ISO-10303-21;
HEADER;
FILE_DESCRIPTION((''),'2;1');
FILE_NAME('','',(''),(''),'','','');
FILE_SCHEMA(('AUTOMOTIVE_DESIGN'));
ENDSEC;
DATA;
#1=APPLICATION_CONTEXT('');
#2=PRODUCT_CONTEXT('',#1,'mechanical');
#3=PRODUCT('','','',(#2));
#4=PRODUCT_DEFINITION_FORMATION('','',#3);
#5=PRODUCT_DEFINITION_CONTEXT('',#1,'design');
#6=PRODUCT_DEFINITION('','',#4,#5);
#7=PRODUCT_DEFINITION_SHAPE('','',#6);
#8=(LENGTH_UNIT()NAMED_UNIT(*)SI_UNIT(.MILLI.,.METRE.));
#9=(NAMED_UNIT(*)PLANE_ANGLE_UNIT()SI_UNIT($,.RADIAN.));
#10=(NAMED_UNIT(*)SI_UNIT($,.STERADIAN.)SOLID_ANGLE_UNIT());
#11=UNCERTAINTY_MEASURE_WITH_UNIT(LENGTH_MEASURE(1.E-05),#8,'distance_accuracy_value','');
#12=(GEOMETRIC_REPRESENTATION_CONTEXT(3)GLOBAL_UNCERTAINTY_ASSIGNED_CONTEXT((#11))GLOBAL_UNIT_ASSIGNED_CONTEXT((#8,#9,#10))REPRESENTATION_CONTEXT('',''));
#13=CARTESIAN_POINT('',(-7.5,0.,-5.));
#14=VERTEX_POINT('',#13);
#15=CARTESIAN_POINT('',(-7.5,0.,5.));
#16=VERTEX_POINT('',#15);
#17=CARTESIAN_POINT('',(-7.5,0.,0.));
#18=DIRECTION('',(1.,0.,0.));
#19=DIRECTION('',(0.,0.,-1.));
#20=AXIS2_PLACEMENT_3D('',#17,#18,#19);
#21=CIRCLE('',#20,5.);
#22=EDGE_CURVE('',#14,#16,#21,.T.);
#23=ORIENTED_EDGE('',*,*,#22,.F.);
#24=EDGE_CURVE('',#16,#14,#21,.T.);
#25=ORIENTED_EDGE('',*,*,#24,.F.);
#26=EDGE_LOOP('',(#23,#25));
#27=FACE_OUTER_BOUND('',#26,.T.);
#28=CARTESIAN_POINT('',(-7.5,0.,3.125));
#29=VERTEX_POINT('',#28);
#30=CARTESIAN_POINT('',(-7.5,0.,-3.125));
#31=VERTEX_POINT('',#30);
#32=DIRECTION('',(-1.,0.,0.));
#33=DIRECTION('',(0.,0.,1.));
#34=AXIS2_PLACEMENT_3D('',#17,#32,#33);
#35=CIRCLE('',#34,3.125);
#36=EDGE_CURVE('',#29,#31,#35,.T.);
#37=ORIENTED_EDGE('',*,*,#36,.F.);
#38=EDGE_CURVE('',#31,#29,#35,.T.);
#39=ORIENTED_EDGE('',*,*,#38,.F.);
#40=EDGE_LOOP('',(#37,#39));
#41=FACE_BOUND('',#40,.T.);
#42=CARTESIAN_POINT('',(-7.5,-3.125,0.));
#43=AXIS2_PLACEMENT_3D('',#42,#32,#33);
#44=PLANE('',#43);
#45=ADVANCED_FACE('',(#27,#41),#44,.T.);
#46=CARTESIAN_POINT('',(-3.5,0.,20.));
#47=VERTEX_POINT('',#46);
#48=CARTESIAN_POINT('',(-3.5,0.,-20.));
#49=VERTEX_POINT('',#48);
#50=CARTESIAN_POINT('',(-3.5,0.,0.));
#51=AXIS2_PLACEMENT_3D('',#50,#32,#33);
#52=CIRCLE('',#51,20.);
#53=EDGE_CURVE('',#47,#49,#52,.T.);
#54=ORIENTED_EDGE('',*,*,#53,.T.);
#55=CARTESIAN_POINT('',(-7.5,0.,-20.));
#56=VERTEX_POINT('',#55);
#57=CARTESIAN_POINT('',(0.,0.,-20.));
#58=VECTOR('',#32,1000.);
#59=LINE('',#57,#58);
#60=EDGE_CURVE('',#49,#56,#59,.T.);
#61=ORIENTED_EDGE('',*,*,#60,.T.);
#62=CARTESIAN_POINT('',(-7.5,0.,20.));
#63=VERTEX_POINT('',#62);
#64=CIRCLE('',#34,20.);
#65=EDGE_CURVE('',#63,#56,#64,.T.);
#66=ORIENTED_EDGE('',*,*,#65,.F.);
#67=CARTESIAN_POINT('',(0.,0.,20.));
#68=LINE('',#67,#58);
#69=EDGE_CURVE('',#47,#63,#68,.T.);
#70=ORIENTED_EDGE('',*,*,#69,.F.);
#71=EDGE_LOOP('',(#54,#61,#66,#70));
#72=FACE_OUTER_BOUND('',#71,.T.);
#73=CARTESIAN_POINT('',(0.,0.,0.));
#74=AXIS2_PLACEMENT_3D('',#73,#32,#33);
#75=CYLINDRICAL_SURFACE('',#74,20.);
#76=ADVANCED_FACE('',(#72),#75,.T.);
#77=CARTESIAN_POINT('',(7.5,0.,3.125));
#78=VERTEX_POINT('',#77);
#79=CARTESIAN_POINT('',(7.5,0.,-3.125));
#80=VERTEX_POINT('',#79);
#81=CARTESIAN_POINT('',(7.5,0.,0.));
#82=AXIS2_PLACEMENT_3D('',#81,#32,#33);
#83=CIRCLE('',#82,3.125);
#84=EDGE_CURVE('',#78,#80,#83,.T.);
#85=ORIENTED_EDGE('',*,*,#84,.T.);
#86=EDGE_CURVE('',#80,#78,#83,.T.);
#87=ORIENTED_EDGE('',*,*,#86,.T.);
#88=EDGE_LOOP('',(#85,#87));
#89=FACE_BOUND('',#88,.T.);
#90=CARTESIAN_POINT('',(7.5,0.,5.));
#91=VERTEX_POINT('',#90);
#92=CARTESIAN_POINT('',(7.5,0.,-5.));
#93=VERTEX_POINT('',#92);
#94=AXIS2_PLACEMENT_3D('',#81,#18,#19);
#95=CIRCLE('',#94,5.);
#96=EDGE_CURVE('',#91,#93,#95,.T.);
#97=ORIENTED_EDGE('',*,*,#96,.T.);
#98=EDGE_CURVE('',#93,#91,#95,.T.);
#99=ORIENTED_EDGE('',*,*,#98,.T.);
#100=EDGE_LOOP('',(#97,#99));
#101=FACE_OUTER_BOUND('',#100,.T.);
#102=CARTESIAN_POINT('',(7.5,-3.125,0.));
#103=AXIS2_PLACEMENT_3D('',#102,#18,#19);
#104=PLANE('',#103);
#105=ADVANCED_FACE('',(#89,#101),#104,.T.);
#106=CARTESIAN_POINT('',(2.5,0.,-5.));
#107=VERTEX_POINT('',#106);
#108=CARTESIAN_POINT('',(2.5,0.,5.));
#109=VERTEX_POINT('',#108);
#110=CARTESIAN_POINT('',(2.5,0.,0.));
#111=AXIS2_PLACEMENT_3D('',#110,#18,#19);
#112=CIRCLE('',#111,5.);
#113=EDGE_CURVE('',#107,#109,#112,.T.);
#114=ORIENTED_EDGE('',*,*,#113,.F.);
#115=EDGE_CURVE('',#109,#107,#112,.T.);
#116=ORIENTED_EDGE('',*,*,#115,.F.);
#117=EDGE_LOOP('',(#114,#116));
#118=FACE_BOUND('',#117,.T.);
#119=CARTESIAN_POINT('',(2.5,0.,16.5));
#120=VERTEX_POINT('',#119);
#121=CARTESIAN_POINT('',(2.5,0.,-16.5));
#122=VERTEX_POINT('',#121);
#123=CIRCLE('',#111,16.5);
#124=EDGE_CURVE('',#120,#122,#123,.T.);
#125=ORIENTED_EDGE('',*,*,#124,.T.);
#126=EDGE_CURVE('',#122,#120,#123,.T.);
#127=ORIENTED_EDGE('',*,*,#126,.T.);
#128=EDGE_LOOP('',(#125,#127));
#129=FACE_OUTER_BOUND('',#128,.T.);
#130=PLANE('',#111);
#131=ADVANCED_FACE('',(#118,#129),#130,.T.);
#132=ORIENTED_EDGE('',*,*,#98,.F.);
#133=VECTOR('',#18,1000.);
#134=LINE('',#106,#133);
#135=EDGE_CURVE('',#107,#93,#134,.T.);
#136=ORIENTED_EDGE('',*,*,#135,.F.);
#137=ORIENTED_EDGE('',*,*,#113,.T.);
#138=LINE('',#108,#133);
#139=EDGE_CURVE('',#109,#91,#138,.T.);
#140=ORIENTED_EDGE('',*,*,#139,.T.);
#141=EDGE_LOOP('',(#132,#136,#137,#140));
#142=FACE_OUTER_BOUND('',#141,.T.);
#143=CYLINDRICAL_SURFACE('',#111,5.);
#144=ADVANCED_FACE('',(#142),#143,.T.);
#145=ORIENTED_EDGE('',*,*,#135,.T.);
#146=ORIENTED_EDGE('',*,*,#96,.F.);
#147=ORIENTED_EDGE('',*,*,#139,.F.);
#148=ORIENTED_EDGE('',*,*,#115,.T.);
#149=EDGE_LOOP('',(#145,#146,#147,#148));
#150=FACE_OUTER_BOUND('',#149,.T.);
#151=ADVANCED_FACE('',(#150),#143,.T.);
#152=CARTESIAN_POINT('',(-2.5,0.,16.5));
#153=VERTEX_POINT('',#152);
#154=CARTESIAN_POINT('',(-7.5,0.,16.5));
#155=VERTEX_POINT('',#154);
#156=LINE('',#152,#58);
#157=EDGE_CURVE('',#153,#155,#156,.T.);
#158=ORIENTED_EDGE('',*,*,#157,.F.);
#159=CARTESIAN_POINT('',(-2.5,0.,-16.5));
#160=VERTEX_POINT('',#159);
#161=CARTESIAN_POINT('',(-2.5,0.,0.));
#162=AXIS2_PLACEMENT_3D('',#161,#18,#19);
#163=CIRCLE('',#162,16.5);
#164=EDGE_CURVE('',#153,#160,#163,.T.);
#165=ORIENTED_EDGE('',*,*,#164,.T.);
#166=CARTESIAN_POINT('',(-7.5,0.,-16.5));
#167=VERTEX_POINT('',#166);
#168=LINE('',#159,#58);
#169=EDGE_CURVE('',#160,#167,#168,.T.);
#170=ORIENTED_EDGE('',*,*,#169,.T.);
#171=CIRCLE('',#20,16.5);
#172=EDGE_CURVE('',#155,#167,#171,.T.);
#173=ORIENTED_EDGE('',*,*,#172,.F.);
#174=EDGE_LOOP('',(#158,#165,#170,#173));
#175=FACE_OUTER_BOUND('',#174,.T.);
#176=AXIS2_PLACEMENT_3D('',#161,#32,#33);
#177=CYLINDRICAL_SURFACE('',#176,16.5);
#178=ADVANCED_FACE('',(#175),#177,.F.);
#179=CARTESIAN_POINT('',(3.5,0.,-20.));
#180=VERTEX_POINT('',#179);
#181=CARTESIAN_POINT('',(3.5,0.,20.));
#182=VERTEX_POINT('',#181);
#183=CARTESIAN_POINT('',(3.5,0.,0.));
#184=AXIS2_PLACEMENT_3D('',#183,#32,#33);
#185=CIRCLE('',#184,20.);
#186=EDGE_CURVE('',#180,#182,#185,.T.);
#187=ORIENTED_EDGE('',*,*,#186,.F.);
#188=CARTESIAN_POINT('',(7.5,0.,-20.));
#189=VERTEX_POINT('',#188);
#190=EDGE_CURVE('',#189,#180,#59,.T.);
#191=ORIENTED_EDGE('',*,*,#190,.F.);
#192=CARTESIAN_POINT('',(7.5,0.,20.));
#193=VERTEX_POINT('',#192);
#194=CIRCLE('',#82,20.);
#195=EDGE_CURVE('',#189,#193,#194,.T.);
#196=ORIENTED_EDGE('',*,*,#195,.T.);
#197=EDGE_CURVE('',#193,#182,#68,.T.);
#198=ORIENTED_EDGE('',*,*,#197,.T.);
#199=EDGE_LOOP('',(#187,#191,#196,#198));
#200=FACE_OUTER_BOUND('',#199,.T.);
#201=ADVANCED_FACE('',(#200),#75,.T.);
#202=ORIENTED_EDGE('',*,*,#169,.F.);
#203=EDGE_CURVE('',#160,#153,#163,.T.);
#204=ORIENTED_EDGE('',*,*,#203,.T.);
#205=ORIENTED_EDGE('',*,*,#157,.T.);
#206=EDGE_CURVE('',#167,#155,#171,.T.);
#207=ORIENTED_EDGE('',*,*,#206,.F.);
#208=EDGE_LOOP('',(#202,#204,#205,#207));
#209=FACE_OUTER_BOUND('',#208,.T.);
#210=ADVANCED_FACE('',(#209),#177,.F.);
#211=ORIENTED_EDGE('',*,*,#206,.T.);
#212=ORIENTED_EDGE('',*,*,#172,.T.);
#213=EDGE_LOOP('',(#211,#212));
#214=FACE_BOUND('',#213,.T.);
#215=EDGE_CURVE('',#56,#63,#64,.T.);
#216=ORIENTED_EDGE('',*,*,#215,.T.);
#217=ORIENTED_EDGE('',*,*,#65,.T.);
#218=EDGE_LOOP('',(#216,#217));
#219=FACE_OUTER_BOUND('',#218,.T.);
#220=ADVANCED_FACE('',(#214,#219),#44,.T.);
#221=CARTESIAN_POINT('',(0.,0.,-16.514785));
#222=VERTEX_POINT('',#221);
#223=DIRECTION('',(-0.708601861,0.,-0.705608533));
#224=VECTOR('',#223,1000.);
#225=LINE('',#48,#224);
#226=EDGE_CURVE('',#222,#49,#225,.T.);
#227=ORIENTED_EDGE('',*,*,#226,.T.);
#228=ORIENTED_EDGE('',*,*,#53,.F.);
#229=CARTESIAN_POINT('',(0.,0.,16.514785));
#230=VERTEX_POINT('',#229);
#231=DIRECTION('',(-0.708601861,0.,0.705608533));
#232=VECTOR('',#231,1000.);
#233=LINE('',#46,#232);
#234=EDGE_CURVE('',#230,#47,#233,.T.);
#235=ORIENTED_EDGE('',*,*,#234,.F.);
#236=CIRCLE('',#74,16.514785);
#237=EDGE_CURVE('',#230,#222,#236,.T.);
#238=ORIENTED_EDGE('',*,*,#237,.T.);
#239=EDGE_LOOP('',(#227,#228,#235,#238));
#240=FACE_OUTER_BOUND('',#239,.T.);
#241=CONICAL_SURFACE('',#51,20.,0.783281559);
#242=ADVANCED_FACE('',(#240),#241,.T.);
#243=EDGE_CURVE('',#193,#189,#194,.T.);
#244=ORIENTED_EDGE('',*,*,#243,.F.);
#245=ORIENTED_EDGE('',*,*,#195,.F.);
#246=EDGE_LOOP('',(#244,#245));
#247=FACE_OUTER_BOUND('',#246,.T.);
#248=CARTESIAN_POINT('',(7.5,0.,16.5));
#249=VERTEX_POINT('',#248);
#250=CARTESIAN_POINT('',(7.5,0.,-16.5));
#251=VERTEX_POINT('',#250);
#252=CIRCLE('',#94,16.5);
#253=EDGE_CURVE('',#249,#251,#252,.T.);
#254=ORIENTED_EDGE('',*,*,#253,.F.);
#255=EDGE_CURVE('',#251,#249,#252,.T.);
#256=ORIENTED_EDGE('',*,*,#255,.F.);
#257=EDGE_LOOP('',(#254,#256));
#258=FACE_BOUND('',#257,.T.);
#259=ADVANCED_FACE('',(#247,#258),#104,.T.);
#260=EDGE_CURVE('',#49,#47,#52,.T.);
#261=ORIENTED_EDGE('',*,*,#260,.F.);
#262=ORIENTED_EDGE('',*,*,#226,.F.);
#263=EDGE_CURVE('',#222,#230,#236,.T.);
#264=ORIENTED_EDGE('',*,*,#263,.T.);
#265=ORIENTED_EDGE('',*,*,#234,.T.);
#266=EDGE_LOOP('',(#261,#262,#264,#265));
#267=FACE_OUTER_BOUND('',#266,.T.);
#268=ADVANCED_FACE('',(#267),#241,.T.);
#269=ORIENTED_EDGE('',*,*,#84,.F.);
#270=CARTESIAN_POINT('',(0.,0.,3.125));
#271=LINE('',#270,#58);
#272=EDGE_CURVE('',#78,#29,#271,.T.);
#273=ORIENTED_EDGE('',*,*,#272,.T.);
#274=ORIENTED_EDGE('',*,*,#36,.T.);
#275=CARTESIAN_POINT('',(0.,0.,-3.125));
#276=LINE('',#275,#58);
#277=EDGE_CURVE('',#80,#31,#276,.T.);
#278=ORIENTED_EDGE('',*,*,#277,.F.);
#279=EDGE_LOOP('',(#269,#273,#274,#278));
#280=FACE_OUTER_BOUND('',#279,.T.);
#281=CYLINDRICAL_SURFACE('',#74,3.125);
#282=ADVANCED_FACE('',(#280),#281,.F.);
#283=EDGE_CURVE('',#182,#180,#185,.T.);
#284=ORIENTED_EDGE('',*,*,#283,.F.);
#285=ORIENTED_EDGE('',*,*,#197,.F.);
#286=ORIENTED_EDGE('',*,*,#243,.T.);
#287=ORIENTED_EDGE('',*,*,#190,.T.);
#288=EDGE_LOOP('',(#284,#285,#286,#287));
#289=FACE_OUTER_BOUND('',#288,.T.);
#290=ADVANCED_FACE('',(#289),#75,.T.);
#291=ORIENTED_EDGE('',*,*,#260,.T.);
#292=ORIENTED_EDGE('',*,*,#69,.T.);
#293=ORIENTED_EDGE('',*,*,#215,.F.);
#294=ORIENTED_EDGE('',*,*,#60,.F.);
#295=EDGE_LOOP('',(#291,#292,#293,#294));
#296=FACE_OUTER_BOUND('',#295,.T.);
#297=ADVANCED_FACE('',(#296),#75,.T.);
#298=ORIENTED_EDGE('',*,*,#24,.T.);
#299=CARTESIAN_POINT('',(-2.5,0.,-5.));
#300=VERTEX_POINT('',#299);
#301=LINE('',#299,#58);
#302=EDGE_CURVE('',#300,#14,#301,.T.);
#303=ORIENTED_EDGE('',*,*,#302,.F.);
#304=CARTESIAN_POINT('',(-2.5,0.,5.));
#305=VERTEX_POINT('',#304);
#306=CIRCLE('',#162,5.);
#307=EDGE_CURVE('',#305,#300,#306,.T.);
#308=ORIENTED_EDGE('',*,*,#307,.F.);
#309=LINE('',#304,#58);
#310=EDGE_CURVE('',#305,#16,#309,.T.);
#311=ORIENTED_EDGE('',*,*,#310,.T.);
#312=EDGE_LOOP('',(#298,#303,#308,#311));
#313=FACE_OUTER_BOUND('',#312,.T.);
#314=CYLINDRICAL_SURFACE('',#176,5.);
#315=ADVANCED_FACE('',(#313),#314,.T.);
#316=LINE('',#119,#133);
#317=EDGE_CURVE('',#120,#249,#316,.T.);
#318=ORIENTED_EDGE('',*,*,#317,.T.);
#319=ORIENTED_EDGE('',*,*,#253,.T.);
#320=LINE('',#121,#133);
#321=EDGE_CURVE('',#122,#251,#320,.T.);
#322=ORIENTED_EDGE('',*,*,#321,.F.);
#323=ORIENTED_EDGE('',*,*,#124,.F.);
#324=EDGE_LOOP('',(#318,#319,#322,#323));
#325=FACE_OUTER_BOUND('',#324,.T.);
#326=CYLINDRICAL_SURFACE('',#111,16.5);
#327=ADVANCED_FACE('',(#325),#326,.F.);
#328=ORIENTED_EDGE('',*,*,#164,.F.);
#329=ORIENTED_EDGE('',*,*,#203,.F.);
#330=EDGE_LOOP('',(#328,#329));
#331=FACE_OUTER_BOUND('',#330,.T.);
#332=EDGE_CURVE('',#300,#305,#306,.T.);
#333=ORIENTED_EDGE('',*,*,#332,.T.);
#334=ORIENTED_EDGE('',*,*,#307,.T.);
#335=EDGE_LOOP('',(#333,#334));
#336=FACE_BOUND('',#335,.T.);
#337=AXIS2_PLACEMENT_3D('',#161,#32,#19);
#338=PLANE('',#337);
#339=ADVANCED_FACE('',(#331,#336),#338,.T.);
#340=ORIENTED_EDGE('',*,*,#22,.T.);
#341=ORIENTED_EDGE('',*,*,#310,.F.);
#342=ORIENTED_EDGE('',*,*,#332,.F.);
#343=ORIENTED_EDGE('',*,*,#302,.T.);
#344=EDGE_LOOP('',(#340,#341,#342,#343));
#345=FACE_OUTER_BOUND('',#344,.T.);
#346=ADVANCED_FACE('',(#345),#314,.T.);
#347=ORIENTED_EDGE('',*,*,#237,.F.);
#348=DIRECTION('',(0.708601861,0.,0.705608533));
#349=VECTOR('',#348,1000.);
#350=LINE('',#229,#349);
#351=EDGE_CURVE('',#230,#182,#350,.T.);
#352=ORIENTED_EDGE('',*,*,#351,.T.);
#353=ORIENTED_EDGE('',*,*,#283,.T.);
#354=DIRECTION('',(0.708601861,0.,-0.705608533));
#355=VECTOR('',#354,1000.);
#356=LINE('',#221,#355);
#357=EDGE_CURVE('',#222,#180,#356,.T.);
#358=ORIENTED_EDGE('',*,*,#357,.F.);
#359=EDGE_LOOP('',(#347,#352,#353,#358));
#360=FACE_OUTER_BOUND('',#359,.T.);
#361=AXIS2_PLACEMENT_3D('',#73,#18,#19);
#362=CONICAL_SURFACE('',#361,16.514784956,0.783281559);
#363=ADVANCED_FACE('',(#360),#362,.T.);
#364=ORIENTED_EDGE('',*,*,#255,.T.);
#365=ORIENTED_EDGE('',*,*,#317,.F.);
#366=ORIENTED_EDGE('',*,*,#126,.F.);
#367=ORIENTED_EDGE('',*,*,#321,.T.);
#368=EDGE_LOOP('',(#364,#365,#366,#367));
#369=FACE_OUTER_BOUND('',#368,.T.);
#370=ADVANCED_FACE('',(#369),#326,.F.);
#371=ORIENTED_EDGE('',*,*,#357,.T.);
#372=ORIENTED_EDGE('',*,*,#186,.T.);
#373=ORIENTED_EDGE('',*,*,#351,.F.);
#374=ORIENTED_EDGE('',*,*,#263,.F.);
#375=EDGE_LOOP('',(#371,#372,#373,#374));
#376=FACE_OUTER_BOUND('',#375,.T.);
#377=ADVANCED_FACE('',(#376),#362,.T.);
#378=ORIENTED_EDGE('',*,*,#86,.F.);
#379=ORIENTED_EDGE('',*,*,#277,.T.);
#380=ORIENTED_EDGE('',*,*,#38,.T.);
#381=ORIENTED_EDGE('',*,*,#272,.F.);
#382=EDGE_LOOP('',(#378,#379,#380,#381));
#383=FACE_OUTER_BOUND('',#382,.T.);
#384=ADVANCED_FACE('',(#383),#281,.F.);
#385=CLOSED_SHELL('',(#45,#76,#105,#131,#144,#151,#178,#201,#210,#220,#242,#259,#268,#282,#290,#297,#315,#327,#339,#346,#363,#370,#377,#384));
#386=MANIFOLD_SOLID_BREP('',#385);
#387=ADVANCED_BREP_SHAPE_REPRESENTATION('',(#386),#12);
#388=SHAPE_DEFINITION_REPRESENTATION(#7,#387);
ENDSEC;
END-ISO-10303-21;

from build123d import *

# Parameters (mm, degrees)
SIDE_RECESS_SKETCH_33_R   = 16.5
SIDE_RECESS_SKETCH_33_R_2 = 5
SIDE_RECESS_33X5_DEPTH    = 5


with BuildPart() as part:
    # Wheel Profile Sketch → Wheel Body (revolve)
    with BuildSketch(Plane.XY, mode=Mode.PRIVATE) as wheel_body_sk:
        Polygon((-7.5, -3.125), (7.5, -3.125), (7.5, -20), (3.5, -20), (0, -16.514784956), (-3.5, -20), (-7.5, -20), align=None)
    revolve(wheel_body_sk.sketch.rotate(Axis((0, 0, 0), (1, 0, 0)), 270), axis=Axis((0, 0, 0), (1, 0, 0)))

    # Side Recess Sketch Ø33 → Side Recess Ø33x5 (cut)
    with BuildSketch(Plane(origin=(7.5, 0, 0), x_dir=(0, 0, -1), z_dir=(1, 0, 0))):
        Circle(SIDE_RECESS_SKETCH_33_R)
        Circle(SIDE_RECESS_SKETCH_33_R_2, mode=Mode.SUBTRACT)
    side_recess_33x5 = extrude(amount=-SIDE_RECESS_33X5_DEPTH, mode=Mode.SUBTRACT)

    # Side Recess Mirror: Side Recess Ø33x5 across plane
    add(side_recess_33x5.mirror(Plane(origin=(0, 0, 0), x_dir=(0, 0, 1), z_dir=(1, 0, 0))), mode=Mode.SUBTRACT)


solid = part.part
